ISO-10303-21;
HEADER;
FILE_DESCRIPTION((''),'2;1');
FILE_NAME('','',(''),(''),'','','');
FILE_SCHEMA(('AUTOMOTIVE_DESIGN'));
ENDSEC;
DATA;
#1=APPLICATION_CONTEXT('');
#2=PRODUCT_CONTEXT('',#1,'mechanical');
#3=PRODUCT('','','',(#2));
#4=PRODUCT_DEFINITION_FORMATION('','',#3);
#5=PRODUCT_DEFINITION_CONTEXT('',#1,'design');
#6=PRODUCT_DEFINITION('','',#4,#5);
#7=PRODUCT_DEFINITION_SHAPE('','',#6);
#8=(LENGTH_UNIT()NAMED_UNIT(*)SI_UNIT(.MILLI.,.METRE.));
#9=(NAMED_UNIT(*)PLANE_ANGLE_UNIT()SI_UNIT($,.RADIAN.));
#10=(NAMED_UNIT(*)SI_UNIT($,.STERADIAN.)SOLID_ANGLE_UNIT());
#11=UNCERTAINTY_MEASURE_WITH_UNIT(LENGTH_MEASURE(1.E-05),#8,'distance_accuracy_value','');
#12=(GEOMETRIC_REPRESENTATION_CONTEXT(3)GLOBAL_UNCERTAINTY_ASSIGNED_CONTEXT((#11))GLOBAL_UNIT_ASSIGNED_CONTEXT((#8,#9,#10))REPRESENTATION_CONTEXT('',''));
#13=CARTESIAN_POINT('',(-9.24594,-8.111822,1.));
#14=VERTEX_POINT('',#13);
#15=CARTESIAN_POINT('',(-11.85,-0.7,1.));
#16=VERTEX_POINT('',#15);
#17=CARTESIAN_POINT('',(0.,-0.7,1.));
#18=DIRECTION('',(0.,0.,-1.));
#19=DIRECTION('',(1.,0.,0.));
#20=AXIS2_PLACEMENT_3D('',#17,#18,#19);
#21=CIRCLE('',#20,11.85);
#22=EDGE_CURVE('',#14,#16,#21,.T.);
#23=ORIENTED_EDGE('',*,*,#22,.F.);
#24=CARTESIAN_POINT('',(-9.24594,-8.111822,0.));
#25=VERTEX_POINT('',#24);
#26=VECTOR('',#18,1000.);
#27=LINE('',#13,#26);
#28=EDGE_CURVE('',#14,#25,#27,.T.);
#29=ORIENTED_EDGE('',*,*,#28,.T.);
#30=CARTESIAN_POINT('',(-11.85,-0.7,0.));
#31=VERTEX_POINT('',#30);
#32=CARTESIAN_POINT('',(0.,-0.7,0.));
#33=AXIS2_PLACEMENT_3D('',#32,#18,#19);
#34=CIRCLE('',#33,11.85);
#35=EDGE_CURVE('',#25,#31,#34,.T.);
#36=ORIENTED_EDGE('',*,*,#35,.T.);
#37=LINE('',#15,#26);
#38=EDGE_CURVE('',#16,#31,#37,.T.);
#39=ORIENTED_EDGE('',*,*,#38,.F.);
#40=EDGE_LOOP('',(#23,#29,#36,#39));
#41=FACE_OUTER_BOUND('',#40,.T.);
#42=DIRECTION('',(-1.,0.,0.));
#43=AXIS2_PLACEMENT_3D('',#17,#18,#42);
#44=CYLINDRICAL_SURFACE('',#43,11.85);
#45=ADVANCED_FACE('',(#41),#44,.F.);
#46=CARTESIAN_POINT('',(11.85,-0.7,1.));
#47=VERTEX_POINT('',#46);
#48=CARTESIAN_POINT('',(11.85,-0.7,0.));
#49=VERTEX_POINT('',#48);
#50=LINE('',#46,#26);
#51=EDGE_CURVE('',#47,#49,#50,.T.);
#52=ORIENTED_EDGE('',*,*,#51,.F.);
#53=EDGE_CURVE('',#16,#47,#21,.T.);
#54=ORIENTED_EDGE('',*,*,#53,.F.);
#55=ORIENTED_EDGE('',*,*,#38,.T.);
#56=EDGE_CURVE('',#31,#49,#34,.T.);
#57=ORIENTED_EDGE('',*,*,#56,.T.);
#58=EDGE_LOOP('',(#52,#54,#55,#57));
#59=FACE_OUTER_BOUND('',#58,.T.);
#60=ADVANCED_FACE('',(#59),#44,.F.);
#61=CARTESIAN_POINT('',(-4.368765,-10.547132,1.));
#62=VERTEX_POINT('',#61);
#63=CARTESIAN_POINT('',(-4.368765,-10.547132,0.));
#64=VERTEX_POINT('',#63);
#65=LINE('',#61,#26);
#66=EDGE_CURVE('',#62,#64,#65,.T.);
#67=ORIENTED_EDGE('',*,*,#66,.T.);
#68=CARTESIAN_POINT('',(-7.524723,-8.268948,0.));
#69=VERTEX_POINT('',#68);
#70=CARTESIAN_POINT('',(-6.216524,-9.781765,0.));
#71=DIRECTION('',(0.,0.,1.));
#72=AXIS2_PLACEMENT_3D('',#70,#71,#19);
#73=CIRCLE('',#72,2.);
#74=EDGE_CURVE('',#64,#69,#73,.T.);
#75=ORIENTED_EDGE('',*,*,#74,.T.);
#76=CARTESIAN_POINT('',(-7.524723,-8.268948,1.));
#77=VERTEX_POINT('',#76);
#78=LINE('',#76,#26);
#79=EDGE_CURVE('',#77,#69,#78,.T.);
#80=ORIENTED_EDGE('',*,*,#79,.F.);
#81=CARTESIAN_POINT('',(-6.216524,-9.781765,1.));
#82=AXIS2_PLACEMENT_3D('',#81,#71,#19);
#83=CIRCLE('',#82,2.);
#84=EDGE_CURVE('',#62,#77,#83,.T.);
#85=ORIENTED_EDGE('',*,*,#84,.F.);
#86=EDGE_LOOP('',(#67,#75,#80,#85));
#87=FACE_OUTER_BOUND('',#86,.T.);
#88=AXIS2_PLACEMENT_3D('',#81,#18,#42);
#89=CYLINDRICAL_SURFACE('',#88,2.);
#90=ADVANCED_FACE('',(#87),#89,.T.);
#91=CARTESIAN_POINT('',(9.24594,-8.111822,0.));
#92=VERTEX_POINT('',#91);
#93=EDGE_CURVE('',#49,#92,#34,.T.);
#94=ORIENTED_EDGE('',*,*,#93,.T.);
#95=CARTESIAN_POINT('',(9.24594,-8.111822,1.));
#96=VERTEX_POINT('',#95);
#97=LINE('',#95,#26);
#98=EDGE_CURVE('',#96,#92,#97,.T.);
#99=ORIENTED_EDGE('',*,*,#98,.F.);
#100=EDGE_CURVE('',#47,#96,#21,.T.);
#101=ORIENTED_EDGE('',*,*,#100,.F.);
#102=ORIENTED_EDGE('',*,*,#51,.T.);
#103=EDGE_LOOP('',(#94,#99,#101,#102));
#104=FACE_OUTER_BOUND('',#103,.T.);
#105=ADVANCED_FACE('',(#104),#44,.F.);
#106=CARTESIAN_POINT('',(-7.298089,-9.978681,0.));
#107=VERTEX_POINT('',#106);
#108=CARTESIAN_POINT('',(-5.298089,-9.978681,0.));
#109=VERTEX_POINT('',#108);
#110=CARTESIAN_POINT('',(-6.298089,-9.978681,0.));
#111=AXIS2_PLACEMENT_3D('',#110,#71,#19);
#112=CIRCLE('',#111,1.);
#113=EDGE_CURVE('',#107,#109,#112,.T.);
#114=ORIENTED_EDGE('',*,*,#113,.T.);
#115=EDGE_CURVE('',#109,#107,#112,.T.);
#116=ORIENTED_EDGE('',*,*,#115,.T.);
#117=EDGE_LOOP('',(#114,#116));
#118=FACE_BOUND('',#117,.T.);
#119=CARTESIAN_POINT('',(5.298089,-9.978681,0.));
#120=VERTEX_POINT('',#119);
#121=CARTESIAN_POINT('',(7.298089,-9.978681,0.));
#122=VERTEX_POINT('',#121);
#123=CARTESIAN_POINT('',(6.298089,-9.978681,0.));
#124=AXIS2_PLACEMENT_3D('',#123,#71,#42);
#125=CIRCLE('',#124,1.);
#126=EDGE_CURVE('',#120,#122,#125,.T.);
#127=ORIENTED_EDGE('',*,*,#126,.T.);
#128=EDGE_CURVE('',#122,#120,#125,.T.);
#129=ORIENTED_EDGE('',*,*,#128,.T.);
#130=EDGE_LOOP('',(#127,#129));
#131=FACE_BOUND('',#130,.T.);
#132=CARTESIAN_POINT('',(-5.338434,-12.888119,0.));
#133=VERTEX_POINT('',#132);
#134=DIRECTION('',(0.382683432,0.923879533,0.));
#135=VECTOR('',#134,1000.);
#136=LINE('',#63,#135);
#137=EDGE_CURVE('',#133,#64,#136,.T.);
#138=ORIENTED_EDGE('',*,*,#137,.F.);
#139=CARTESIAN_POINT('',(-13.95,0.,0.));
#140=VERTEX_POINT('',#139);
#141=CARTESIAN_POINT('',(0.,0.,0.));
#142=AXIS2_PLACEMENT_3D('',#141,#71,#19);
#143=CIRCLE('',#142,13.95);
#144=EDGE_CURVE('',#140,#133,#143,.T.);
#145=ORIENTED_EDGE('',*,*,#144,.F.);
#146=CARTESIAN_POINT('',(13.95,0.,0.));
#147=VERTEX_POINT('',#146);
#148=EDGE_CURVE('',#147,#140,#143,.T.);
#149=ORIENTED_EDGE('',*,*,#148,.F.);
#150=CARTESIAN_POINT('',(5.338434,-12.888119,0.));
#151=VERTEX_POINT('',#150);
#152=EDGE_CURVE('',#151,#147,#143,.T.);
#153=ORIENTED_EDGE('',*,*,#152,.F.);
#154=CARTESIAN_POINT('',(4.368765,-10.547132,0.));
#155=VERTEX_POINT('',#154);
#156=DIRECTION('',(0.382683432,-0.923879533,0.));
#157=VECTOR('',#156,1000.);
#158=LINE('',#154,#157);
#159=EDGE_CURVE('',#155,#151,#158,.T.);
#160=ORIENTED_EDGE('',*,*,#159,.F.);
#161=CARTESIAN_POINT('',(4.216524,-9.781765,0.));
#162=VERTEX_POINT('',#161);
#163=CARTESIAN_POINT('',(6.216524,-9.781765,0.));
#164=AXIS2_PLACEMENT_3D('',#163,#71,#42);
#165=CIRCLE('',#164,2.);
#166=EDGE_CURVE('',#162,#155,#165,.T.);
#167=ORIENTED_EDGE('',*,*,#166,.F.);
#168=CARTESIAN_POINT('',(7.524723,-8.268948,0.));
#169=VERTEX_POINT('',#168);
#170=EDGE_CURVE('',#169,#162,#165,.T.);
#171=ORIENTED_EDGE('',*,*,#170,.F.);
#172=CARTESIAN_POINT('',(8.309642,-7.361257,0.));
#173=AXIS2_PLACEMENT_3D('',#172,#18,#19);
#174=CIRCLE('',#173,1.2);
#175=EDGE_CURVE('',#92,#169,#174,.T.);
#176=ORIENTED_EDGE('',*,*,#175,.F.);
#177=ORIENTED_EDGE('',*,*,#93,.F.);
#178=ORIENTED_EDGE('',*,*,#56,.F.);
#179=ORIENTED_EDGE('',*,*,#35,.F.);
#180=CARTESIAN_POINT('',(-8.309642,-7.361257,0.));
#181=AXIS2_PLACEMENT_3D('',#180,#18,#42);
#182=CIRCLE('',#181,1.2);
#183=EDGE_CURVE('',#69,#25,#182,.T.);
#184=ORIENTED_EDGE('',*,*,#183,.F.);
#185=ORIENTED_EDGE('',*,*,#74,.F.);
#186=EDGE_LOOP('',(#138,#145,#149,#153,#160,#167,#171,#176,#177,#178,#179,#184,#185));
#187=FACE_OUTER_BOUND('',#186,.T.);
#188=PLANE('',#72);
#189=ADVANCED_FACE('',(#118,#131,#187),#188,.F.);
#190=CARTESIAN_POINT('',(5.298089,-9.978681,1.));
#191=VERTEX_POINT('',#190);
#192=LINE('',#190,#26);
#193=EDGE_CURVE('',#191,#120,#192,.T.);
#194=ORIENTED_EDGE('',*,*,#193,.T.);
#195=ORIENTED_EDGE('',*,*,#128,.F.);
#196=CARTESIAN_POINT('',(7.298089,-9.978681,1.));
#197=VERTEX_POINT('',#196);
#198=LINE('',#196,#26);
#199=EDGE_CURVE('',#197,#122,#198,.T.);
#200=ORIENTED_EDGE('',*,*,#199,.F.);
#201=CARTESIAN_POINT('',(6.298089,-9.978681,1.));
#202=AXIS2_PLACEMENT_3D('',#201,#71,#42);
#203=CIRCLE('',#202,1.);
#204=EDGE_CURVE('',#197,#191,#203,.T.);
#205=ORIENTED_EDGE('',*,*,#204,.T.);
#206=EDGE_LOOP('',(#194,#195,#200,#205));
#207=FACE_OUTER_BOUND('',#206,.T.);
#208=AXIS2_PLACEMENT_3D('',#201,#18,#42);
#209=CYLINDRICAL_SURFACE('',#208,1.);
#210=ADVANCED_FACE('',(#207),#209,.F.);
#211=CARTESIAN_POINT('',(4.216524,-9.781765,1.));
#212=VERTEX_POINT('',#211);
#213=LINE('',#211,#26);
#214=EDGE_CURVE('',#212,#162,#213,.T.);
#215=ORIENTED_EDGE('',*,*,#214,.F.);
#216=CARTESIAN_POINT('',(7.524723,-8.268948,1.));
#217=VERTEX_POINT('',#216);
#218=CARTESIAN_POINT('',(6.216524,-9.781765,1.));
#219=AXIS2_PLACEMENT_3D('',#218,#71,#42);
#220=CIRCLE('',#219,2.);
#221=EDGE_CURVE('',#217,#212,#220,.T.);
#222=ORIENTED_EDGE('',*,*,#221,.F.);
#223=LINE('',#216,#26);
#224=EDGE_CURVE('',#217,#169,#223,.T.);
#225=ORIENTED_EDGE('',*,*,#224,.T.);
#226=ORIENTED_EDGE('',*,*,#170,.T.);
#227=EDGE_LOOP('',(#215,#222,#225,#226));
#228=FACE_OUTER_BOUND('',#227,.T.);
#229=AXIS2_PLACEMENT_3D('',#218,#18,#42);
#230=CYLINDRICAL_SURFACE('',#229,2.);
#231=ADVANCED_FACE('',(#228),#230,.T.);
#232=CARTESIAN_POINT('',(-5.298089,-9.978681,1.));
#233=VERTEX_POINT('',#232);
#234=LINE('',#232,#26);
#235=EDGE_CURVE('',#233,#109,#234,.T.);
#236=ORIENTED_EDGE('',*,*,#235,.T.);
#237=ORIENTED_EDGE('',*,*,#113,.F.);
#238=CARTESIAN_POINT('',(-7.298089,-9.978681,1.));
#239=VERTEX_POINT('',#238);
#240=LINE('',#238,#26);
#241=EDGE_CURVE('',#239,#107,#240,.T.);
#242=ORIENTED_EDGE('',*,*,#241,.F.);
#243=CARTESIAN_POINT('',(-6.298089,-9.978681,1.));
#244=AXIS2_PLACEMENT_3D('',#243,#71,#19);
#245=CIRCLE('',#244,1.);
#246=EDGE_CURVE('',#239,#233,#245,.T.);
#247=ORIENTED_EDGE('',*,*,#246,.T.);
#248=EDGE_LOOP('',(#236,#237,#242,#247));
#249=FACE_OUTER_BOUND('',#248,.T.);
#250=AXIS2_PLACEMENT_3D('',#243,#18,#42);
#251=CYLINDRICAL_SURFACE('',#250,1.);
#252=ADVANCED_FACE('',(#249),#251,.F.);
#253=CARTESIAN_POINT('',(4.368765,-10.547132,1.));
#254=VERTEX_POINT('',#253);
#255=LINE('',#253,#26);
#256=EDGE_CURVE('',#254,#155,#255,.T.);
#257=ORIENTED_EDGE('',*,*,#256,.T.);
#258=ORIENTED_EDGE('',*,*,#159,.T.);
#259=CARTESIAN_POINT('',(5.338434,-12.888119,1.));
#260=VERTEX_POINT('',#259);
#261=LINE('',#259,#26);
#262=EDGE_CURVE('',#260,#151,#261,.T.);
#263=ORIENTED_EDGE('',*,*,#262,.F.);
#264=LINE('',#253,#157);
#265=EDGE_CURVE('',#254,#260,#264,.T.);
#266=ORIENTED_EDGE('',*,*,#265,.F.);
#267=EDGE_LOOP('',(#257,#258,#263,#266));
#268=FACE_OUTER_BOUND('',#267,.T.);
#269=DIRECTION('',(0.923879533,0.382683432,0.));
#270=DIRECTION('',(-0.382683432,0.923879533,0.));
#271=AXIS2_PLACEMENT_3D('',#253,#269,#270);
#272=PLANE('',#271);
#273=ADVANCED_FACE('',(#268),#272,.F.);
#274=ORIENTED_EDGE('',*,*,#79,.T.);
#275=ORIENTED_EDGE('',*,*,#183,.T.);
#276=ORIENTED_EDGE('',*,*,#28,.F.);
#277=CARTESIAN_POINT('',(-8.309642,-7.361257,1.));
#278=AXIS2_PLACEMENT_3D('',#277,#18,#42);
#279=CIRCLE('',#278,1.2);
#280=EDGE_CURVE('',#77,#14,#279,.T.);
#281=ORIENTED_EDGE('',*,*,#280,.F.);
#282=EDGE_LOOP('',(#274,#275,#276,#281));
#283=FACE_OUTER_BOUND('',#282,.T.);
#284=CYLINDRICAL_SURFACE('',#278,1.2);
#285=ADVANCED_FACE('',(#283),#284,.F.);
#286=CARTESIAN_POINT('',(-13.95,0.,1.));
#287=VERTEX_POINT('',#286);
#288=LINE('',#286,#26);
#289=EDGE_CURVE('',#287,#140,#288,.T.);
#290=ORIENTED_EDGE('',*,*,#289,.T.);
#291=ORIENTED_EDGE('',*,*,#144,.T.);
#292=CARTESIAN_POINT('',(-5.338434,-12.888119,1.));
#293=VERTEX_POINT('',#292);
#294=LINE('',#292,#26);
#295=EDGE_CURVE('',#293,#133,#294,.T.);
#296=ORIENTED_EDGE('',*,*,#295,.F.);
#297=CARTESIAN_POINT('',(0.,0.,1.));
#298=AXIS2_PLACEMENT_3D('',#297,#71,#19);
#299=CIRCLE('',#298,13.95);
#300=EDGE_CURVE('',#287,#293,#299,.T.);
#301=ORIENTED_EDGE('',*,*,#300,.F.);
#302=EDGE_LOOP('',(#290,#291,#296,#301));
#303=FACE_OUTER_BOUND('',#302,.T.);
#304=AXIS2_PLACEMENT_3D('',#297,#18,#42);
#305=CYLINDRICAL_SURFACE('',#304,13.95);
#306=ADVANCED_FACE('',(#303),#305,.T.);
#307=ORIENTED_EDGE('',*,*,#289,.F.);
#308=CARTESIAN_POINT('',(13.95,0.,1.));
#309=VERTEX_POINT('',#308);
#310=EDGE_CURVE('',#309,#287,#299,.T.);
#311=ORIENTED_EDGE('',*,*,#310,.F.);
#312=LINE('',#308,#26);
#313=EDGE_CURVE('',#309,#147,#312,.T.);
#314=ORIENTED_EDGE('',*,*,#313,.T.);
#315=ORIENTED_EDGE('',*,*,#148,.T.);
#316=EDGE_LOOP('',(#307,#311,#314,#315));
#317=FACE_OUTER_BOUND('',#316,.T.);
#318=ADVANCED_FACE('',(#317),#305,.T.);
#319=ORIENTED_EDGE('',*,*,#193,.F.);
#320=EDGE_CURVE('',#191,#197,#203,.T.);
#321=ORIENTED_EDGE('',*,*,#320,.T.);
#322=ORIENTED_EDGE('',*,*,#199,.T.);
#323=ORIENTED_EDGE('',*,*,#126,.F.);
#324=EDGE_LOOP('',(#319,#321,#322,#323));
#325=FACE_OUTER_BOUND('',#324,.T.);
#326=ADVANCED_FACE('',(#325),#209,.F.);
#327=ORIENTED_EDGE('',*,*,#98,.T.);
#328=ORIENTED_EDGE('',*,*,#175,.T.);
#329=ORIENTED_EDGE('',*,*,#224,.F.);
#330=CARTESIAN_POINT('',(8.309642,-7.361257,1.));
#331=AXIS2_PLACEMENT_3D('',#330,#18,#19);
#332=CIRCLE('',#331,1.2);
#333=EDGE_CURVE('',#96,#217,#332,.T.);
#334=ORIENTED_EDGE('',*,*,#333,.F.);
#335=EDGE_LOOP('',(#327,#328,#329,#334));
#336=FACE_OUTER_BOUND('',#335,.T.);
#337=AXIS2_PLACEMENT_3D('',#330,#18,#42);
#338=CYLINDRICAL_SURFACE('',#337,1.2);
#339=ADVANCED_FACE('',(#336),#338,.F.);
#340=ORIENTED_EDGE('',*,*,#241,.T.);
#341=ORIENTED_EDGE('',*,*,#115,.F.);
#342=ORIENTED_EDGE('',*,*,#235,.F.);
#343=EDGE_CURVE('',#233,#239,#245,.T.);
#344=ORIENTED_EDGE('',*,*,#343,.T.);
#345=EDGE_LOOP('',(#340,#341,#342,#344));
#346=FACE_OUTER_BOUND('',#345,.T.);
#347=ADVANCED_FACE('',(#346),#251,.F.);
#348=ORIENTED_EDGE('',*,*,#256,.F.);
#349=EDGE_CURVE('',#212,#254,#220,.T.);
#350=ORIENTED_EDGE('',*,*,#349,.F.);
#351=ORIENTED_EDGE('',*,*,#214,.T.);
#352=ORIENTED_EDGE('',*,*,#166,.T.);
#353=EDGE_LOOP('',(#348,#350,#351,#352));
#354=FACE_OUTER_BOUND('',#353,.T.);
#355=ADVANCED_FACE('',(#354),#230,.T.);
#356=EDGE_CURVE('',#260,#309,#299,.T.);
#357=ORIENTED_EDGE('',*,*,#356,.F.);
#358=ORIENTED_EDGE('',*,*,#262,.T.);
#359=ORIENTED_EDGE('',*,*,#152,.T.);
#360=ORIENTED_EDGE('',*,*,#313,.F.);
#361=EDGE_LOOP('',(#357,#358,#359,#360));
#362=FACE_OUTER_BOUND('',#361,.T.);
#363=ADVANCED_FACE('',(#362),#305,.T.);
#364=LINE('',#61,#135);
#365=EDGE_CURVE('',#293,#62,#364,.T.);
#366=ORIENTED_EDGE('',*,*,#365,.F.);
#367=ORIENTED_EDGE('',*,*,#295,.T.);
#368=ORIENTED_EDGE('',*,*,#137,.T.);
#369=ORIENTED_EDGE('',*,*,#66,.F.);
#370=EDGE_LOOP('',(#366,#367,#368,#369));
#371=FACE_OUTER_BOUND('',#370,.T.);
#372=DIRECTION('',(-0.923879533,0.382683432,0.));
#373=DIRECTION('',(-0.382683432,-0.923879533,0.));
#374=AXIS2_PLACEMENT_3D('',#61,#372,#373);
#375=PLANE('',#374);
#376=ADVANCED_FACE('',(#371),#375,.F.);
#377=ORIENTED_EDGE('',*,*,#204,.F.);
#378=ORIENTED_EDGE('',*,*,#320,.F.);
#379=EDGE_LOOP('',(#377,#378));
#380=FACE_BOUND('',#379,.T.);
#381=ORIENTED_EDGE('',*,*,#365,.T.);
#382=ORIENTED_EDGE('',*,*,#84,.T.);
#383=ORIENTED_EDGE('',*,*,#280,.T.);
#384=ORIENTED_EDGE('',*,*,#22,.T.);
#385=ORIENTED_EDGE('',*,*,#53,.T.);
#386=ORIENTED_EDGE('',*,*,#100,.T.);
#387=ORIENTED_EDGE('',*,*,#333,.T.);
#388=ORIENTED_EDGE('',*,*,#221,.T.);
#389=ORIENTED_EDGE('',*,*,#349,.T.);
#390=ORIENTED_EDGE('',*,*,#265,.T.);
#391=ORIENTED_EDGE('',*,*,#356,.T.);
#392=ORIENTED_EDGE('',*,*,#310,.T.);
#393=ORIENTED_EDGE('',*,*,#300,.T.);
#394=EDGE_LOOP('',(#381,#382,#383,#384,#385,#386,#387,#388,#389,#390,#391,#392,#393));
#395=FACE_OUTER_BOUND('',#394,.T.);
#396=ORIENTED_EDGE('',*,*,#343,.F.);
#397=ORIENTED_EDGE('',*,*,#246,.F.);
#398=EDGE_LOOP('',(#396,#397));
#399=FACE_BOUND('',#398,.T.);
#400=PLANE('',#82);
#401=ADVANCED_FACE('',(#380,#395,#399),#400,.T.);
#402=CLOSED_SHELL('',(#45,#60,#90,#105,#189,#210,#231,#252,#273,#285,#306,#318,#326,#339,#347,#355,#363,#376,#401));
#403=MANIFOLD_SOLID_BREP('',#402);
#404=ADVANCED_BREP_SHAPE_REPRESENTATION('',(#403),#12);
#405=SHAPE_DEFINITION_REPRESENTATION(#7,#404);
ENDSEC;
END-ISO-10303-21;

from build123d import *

# Parameters (mm, degrees)
SKETCH_1_R        = 1
EXTRUDE_967_DEPTH = 1


with BuildPart() as part:
    # 草图1 → Extrude 967 (new body)
    with BuildSketch(Plane.XY):
        with BuildLine():
            Line((-4.368765084, -10.547131916), (-5.338433881, -12.888119479))
            ThreePointArc((-5.338433881, -12.888119479), (0, 13.95), (5.338433881, -12.888119479))
            Line((5.338433881, -12.888119479), (4.368765084, -10.547131916))
            ThreePointArc((4.368765084, -10.547131916), (5.045920823, -8.160133818), (7.524722821, -8.268947735))
            ThreePointArc((7.524722821, -8.268947735), (8.418733826, -8.556288298), (9.245939718, -8.111821553))
            ThreePointArc((9.245939718, -8.111821553), (0, 11.15), (-9.245939718, -8.111821553))
            ThreePointArc((-9.245939718, -8.111821553), (-8.418733826, -8.556288298), (-7.524722821, -8.268947735))
            ThreePointArc((-7.524722821, -8.268947735), (-5.045920823, -8.160133818), (-4.368765084, -10.547131916))
        make_face()
        with Locations((-6.298089329, -9.978680815)):
            Circle(SKETCH_1_R, mode=Mode.SUBTRACT)
        with Locations(Location((6.298089329, -9.978680815, 0), (0, 0, 180))):
            Circle(SKETCH_1_R, mode=Mode.SUBTRACT)
    extrude(amount=EXTRUDE_967_DEPTH)


solid = part.part
